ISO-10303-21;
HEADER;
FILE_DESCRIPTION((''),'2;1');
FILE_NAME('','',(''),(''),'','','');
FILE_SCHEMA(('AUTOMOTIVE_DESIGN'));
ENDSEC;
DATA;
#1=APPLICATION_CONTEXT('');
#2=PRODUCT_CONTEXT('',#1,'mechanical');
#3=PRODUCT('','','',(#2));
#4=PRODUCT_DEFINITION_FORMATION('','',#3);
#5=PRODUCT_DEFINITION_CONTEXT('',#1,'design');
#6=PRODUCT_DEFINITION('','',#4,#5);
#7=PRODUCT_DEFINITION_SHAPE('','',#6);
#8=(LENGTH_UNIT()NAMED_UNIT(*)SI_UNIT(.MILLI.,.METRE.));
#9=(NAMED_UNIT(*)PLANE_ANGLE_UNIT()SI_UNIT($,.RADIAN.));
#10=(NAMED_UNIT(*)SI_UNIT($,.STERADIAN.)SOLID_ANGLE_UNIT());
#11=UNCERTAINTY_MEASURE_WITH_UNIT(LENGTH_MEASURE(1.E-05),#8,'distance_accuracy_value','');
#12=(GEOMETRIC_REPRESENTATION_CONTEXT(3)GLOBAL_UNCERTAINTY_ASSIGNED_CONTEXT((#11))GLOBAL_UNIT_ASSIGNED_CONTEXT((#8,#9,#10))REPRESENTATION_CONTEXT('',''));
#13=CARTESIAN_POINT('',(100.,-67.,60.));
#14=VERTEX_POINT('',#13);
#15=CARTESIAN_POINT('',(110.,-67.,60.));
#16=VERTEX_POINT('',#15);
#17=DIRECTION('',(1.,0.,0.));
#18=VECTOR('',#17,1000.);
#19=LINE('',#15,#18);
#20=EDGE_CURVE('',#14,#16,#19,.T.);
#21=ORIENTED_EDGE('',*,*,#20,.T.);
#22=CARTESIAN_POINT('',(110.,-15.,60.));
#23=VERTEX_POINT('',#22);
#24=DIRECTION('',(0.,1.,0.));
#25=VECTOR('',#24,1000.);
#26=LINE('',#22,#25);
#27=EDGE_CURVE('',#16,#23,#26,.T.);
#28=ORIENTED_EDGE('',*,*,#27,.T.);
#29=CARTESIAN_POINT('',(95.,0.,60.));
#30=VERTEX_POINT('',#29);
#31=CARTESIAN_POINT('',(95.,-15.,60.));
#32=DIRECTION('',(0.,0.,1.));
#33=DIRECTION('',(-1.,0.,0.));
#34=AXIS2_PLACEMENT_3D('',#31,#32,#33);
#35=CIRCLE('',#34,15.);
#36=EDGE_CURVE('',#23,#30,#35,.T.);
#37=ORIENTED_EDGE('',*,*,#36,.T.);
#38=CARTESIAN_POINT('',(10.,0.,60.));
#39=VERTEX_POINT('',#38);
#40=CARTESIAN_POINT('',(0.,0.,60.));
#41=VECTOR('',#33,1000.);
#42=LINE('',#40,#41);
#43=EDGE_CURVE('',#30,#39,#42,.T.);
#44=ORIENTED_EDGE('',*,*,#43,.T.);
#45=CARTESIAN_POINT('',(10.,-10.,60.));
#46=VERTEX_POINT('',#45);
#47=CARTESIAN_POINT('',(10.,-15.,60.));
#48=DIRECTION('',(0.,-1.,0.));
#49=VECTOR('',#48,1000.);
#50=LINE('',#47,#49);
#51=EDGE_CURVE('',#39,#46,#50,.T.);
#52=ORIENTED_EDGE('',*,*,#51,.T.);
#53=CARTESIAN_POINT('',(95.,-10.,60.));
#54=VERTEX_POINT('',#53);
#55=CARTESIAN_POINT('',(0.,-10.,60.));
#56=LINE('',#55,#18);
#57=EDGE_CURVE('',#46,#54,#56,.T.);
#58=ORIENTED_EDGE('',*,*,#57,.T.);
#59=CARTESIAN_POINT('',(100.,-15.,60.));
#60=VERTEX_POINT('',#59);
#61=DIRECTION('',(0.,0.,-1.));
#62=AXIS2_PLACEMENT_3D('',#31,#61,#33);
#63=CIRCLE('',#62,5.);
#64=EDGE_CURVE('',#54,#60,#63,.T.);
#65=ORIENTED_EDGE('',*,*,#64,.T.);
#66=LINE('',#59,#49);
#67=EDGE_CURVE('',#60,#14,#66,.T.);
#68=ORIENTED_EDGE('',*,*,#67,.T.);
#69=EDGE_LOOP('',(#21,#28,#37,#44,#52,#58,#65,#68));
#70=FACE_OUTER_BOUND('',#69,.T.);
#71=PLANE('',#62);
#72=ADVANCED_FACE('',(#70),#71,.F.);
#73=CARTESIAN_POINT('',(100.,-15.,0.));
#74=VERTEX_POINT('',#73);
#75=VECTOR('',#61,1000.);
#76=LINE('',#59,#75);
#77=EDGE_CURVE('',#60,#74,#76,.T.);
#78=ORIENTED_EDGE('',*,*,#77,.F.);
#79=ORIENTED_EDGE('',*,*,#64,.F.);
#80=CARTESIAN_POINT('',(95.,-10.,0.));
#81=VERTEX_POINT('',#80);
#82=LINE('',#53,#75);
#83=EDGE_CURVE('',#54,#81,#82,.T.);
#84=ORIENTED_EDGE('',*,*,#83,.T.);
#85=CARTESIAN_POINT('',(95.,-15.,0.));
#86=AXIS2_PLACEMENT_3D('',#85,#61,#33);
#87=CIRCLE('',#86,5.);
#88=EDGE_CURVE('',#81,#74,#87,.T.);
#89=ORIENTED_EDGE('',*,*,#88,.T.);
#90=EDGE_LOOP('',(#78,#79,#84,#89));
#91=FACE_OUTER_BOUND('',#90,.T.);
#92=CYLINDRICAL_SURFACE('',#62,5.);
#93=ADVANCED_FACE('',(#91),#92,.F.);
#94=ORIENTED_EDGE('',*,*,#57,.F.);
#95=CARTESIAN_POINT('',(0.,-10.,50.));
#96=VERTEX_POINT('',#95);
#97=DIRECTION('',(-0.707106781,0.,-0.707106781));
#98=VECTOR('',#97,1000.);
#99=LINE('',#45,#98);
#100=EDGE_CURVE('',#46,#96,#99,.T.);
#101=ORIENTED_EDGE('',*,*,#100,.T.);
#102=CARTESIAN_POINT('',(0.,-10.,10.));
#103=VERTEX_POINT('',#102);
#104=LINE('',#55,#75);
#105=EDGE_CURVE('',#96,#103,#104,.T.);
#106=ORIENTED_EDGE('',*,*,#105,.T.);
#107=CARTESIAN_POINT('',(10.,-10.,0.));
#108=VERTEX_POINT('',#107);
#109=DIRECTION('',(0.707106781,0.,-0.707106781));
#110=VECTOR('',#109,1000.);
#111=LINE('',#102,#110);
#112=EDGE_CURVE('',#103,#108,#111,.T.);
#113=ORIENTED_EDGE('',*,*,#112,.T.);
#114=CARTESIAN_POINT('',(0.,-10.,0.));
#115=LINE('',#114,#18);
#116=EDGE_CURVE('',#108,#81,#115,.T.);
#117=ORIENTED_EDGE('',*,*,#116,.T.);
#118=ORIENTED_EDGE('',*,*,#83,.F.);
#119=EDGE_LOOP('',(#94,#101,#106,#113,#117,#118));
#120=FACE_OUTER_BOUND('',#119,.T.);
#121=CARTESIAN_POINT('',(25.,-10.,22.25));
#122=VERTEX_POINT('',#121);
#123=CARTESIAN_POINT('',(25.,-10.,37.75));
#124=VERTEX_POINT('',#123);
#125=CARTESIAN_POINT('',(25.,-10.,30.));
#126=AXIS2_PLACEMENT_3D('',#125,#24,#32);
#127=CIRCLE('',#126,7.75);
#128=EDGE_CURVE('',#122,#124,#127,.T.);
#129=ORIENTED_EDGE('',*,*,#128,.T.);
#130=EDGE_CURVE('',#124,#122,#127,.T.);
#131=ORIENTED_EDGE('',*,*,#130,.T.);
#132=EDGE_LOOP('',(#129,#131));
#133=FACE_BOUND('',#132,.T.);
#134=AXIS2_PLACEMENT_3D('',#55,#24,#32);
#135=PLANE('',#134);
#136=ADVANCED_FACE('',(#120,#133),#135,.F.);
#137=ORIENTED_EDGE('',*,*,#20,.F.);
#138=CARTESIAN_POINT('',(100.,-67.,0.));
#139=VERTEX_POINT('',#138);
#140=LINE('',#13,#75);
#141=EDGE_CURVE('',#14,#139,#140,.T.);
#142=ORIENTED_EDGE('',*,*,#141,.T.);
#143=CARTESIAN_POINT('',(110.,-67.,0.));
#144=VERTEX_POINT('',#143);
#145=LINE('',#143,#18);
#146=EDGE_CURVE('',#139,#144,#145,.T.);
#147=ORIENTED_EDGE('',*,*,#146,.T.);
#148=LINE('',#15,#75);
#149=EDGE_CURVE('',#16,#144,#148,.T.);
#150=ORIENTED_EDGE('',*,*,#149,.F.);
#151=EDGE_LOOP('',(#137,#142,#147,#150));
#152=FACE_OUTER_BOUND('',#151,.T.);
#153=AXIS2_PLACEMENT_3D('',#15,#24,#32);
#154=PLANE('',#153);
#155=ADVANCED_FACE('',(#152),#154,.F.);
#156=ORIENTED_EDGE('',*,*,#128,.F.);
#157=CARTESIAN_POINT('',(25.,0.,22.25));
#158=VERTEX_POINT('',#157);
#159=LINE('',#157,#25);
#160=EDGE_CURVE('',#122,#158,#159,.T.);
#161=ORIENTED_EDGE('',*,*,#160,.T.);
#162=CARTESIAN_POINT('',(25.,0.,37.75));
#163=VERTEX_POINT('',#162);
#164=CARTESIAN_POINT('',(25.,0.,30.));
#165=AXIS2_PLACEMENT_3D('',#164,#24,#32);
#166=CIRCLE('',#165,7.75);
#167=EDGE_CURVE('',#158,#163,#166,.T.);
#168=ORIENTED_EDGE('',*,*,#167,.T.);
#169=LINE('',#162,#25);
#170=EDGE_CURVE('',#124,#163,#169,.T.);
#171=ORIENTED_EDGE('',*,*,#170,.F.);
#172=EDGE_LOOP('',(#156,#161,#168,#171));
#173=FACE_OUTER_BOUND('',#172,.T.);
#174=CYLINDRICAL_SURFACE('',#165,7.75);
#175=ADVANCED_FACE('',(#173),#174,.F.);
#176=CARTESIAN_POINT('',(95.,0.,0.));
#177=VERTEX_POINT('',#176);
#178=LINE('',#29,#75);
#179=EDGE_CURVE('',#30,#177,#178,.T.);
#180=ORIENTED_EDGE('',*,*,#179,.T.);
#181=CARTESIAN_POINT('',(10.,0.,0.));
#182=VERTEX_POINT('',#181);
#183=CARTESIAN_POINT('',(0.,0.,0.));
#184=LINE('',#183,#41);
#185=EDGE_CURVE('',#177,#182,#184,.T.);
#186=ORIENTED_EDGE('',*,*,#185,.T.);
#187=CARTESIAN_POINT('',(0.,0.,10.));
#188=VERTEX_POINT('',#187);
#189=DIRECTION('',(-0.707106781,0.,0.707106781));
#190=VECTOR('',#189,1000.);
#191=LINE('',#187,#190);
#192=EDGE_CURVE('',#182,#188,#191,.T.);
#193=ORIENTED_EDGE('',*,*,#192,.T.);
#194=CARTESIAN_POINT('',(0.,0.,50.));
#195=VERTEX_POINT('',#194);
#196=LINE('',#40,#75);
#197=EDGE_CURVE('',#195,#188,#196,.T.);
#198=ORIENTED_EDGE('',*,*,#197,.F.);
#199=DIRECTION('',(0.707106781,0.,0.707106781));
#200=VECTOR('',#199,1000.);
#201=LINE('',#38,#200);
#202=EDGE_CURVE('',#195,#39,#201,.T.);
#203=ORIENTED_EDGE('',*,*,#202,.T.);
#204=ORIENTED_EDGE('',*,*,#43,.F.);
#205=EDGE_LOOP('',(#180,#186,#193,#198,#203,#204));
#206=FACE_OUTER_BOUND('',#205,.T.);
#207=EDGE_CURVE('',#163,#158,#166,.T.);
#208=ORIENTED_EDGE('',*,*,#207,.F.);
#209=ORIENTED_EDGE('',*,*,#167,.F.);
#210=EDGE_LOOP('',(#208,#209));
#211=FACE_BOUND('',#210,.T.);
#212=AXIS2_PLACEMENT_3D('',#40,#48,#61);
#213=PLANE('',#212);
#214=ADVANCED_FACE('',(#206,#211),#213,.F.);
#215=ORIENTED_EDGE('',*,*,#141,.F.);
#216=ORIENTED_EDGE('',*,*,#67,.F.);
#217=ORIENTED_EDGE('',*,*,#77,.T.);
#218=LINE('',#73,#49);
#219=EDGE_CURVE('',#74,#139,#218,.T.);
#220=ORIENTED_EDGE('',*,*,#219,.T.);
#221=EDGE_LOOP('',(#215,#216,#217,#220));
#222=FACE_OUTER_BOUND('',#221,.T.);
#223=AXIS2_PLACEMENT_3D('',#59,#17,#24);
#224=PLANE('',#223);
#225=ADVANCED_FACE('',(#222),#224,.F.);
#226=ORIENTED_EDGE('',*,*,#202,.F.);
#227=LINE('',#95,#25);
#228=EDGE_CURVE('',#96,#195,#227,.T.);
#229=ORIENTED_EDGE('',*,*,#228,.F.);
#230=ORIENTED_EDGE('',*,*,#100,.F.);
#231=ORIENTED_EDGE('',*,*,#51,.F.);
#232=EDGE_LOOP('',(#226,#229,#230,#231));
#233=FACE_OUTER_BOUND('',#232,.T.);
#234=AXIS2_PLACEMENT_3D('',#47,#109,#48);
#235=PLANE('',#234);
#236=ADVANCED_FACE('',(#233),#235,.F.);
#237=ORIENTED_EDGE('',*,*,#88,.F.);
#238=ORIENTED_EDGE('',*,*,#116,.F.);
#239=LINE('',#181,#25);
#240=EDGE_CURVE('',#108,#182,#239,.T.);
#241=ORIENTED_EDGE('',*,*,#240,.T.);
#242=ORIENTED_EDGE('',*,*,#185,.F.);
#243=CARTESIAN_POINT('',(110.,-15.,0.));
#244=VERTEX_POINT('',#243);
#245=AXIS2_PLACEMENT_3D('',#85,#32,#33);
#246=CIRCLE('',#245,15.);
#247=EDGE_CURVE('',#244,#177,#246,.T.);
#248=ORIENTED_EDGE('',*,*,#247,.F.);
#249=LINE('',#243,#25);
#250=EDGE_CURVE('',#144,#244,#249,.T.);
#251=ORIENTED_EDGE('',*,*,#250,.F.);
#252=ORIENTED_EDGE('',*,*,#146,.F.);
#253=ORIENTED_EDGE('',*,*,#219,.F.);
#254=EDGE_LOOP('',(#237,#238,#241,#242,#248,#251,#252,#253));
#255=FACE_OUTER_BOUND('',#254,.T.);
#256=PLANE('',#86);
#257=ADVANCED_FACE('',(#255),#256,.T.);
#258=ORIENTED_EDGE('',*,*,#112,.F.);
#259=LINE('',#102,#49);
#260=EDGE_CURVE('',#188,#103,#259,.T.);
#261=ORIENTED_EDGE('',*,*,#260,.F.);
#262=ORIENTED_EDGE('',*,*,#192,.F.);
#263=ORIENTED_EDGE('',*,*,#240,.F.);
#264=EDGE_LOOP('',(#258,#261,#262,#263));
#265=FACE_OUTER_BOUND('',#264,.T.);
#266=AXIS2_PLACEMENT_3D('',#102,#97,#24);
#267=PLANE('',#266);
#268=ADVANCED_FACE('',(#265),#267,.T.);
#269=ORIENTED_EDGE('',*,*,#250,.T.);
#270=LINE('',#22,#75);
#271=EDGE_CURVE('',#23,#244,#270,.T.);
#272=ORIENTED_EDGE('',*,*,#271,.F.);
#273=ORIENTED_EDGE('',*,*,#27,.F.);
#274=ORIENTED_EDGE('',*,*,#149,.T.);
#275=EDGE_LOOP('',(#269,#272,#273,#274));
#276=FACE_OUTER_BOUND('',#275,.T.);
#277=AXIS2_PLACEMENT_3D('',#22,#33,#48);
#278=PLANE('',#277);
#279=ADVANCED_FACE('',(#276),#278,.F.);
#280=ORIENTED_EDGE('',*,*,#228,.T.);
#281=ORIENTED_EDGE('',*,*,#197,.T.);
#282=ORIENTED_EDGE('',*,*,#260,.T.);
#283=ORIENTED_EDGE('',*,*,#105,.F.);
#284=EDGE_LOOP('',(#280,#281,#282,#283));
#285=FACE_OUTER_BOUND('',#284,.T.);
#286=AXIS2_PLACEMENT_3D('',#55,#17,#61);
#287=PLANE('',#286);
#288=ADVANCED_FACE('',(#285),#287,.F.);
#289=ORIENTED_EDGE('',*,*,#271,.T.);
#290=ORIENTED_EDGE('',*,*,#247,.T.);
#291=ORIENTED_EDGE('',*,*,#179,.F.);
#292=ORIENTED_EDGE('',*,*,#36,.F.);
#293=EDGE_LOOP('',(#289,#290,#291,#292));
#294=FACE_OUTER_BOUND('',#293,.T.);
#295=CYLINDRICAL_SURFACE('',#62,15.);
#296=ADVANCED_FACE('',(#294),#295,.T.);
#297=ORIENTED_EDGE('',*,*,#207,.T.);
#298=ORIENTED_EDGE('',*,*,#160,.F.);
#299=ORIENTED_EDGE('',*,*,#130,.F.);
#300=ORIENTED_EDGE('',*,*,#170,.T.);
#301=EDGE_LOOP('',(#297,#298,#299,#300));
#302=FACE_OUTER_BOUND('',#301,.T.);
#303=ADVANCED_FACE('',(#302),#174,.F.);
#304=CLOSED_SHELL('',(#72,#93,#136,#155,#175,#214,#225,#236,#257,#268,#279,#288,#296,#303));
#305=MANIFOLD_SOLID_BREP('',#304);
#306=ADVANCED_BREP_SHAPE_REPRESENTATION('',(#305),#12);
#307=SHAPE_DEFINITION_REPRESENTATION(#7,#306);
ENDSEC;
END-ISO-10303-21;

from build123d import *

# Parameters (mm, degrees)
BOSS_EXTRUDE1_DEPTH    = 60
CHAMFER1_SIZE          = 10
M18_TAPPED_HOLE1_D     = 15.5
M18_TAPPED_HOLE1_DEPTH = 43.5
M18_TAPPED_HOLE1_TIP   = 4.656669797


with BuildPart() as part:
    # Sketch1 → Boss-Extrude1 (new body)
    with BuildSketch(Plane.XY):
        with BuildLine():
            Line((0, 0), (95, 0))
            ThreePointArc((95, 0), (105.606601718, -4.393398282), (110, -15))
            Line((110, -15), (110, -67))
            Line((110, -67), (100, -67))
            Line((100, -67), (100, -15))
            ThreePointArc((100, -15), (98.535533906, -11.464466094), (95, -10))
            Line((95, -10), (0, -10))
            Line((0, -10), (0, 0))
        make_face()
    extrude(amount=BOSS_EXTRUDE1_DEPTH)

    # Chamfer1
    chamfer1_edges = [part.edges().sort_by_distance(p)[0] for p in [
        (0, -5, 0),
        (0, -5, 60),
    ]]
    chamfer(chamfer1_edges, length=CHAMFER1_SIZE)

    # M18 Tapped Hole1
    with Locations(Plane(origin=(0, 0, 0), x_dir=(1, 0, 0), z_dir=(0, 1, 0))):
        with Locations((25, -30)):
            Hole(M18_TAPPED_HOLE1_D / 2, depth=M18_TAPPED_HOLE1_DEPTH)
            with Locations((0, 0, -(M18_TAPPED_HOLE1_DEPTH + M18_TAPPED_HOLE1_TIP / 2))):  # 118° drill point
                Cone(0, M18_TAPPED_HOLE1_D / 2, M18_TAPPED_HOLE1_TIP, mode=Mode.SUBTRACT)


solid = part.part
